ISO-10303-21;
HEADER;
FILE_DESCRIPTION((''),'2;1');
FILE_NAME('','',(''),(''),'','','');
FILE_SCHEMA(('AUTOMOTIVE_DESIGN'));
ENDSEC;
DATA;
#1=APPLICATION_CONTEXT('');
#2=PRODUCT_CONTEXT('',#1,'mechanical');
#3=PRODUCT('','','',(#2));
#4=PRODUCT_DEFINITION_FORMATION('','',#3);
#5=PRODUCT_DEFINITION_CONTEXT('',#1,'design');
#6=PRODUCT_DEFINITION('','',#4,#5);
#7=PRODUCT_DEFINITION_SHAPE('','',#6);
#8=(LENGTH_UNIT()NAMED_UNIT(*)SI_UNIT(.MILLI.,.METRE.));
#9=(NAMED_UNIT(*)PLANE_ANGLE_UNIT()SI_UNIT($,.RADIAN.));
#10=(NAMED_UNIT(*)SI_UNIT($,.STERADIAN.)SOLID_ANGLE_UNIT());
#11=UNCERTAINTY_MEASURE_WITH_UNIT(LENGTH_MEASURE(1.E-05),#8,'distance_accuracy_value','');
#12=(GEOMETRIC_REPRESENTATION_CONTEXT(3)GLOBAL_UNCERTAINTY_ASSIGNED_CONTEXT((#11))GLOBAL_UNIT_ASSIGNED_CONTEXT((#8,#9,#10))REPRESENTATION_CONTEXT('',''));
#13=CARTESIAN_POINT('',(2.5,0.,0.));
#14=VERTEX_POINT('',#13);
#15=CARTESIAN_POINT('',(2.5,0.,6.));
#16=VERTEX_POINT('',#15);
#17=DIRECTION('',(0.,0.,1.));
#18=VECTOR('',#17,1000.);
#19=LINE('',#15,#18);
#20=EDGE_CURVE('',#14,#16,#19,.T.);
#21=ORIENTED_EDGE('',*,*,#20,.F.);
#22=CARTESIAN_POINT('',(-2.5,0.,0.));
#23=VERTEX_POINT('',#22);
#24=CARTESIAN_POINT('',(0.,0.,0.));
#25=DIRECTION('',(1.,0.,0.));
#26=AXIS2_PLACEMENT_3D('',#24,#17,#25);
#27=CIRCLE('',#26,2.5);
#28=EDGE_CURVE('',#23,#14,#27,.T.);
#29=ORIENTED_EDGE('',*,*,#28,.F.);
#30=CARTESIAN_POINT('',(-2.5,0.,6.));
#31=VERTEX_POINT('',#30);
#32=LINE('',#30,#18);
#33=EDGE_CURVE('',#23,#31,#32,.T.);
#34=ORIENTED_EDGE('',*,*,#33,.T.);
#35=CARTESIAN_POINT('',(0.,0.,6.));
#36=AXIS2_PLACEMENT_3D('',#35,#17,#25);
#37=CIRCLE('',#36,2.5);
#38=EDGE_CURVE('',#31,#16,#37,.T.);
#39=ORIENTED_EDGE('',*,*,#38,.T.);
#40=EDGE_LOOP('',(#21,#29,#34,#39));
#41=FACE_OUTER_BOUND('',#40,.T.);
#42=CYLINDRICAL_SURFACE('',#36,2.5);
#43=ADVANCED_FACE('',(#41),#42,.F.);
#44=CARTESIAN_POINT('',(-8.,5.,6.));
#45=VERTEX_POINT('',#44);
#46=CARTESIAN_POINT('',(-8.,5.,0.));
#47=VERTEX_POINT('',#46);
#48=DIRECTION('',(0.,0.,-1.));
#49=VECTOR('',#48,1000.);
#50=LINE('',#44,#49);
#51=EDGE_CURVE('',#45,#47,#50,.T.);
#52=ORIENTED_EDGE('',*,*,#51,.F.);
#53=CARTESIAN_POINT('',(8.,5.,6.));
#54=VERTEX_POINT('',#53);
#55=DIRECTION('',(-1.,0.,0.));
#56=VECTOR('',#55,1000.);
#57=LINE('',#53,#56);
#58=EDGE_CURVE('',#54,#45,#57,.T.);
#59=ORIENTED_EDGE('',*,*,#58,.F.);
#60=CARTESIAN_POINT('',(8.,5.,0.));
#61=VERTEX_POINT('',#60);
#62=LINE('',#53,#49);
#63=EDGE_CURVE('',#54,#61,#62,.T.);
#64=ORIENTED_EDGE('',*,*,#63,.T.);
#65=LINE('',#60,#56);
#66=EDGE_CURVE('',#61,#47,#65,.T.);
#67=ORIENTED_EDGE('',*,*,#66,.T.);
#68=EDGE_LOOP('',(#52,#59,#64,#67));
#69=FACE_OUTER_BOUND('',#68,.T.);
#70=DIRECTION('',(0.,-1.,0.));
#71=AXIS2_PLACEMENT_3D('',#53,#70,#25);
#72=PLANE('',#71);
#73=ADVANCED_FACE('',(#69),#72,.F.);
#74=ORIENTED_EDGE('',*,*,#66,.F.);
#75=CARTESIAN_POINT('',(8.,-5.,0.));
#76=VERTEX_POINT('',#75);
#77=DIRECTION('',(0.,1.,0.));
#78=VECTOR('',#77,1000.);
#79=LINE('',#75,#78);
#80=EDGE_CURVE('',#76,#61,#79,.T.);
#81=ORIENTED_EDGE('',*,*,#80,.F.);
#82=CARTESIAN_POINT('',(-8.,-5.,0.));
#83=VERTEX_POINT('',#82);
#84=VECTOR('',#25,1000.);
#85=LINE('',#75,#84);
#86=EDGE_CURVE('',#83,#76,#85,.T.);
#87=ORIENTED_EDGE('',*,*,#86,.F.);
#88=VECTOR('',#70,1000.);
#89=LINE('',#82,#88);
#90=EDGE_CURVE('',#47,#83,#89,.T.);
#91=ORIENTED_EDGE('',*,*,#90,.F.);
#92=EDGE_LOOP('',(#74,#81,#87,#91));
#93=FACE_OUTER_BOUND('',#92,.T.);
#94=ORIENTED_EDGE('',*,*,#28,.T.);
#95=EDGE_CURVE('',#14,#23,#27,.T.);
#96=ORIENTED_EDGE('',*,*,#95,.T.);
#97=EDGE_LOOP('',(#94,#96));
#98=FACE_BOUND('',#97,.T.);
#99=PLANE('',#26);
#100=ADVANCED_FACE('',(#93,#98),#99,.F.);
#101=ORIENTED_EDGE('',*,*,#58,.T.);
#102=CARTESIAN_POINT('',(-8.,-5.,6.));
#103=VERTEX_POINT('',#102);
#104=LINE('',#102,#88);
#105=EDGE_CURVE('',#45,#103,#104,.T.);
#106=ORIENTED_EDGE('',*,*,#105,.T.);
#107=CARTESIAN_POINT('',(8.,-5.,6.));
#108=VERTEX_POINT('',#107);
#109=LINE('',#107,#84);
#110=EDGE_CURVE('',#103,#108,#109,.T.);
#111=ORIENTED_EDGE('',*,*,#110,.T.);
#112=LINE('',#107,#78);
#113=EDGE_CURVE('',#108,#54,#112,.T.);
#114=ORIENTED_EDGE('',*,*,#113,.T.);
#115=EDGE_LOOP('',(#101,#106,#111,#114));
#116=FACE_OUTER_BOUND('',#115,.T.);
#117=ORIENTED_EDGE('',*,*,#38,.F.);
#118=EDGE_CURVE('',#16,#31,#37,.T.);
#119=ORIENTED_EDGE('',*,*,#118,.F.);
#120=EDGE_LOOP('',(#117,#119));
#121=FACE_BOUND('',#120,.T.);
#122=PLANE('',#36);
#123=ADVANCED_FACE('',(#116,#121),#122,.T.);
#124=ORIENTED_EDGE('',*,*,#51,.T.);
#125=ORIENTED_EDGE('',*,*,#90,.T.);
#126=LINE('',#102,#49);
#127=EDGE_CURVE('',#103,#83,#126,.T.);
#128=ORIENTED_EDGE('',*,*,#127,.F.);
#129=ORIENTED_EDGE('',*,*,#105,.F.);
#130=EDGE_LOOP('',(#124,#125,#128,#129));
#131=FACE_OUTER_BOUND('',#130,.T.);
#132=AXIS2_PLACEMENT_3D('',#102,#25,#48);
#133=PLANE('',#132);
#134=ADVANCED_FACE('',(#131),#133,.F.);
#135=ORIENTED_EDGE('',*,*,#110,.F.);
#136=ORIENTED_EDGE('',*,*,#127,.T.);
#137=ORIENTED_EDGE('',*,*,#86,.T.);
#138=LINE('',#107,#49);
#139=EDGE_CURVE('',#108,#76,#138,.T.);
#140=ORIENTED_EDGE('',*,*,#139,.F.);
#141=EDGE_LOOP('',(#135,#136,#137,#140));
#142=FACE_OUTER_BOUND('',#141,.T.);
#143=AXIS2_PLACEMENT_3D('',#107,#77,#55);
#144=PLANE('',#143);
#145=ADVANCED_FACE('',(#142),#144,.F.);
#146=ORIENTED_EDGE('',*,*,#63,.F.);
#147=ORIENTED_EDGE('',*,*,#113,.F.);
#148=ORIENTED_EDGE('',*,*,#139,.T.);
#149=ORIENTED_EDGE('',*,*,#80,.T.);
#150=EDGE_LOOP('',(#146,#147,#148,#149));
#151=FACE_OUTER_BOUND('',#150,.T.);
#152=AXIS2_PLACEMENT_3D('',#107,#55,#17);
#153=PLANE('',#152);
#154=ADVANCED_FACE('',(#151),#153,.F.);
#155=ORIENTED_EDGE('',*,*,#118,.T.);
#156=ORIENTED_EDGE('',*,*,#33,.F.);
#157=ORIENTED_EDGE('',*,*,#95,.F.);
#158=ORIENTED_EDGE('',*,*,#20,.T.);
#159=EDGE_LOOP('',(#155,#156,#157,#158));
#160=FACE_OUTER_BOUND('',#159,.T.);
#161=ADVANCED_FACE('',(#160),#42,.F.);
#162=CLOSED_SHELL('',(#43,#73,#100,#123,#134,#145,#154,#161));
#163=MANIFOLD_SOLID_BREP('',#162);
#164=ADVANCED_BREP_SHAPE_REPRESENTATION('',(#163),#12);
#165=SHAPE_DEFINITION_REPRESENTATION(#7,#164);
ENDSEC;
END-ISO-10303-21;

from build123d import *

# Parameters (mm, degrees)
SKETCH1_W           = 16
SKETCH1_H           = 10
BOSS_EXTRUDE1_DEPTH = 6
M6_TAPPED_HOLE1_D   = 5


with BuildPart() as part:
    # Sketch1 → Boss-Extrude1 (new body)
    with BuildSketch(Plane.XY):
        Rectangle(SKETCH1_W, SKETCH1_H)
    extrude(amount=BOSS_EXTRUDE1_DEPTH)

    # M6 Tapped Hole1 (through all)
    with Locations(Plane.XY.offset(6)):
        with Locations((0, 0)):
            Hole(M6_TAPPED_HOLE1_D / 2)


solid = part.part
